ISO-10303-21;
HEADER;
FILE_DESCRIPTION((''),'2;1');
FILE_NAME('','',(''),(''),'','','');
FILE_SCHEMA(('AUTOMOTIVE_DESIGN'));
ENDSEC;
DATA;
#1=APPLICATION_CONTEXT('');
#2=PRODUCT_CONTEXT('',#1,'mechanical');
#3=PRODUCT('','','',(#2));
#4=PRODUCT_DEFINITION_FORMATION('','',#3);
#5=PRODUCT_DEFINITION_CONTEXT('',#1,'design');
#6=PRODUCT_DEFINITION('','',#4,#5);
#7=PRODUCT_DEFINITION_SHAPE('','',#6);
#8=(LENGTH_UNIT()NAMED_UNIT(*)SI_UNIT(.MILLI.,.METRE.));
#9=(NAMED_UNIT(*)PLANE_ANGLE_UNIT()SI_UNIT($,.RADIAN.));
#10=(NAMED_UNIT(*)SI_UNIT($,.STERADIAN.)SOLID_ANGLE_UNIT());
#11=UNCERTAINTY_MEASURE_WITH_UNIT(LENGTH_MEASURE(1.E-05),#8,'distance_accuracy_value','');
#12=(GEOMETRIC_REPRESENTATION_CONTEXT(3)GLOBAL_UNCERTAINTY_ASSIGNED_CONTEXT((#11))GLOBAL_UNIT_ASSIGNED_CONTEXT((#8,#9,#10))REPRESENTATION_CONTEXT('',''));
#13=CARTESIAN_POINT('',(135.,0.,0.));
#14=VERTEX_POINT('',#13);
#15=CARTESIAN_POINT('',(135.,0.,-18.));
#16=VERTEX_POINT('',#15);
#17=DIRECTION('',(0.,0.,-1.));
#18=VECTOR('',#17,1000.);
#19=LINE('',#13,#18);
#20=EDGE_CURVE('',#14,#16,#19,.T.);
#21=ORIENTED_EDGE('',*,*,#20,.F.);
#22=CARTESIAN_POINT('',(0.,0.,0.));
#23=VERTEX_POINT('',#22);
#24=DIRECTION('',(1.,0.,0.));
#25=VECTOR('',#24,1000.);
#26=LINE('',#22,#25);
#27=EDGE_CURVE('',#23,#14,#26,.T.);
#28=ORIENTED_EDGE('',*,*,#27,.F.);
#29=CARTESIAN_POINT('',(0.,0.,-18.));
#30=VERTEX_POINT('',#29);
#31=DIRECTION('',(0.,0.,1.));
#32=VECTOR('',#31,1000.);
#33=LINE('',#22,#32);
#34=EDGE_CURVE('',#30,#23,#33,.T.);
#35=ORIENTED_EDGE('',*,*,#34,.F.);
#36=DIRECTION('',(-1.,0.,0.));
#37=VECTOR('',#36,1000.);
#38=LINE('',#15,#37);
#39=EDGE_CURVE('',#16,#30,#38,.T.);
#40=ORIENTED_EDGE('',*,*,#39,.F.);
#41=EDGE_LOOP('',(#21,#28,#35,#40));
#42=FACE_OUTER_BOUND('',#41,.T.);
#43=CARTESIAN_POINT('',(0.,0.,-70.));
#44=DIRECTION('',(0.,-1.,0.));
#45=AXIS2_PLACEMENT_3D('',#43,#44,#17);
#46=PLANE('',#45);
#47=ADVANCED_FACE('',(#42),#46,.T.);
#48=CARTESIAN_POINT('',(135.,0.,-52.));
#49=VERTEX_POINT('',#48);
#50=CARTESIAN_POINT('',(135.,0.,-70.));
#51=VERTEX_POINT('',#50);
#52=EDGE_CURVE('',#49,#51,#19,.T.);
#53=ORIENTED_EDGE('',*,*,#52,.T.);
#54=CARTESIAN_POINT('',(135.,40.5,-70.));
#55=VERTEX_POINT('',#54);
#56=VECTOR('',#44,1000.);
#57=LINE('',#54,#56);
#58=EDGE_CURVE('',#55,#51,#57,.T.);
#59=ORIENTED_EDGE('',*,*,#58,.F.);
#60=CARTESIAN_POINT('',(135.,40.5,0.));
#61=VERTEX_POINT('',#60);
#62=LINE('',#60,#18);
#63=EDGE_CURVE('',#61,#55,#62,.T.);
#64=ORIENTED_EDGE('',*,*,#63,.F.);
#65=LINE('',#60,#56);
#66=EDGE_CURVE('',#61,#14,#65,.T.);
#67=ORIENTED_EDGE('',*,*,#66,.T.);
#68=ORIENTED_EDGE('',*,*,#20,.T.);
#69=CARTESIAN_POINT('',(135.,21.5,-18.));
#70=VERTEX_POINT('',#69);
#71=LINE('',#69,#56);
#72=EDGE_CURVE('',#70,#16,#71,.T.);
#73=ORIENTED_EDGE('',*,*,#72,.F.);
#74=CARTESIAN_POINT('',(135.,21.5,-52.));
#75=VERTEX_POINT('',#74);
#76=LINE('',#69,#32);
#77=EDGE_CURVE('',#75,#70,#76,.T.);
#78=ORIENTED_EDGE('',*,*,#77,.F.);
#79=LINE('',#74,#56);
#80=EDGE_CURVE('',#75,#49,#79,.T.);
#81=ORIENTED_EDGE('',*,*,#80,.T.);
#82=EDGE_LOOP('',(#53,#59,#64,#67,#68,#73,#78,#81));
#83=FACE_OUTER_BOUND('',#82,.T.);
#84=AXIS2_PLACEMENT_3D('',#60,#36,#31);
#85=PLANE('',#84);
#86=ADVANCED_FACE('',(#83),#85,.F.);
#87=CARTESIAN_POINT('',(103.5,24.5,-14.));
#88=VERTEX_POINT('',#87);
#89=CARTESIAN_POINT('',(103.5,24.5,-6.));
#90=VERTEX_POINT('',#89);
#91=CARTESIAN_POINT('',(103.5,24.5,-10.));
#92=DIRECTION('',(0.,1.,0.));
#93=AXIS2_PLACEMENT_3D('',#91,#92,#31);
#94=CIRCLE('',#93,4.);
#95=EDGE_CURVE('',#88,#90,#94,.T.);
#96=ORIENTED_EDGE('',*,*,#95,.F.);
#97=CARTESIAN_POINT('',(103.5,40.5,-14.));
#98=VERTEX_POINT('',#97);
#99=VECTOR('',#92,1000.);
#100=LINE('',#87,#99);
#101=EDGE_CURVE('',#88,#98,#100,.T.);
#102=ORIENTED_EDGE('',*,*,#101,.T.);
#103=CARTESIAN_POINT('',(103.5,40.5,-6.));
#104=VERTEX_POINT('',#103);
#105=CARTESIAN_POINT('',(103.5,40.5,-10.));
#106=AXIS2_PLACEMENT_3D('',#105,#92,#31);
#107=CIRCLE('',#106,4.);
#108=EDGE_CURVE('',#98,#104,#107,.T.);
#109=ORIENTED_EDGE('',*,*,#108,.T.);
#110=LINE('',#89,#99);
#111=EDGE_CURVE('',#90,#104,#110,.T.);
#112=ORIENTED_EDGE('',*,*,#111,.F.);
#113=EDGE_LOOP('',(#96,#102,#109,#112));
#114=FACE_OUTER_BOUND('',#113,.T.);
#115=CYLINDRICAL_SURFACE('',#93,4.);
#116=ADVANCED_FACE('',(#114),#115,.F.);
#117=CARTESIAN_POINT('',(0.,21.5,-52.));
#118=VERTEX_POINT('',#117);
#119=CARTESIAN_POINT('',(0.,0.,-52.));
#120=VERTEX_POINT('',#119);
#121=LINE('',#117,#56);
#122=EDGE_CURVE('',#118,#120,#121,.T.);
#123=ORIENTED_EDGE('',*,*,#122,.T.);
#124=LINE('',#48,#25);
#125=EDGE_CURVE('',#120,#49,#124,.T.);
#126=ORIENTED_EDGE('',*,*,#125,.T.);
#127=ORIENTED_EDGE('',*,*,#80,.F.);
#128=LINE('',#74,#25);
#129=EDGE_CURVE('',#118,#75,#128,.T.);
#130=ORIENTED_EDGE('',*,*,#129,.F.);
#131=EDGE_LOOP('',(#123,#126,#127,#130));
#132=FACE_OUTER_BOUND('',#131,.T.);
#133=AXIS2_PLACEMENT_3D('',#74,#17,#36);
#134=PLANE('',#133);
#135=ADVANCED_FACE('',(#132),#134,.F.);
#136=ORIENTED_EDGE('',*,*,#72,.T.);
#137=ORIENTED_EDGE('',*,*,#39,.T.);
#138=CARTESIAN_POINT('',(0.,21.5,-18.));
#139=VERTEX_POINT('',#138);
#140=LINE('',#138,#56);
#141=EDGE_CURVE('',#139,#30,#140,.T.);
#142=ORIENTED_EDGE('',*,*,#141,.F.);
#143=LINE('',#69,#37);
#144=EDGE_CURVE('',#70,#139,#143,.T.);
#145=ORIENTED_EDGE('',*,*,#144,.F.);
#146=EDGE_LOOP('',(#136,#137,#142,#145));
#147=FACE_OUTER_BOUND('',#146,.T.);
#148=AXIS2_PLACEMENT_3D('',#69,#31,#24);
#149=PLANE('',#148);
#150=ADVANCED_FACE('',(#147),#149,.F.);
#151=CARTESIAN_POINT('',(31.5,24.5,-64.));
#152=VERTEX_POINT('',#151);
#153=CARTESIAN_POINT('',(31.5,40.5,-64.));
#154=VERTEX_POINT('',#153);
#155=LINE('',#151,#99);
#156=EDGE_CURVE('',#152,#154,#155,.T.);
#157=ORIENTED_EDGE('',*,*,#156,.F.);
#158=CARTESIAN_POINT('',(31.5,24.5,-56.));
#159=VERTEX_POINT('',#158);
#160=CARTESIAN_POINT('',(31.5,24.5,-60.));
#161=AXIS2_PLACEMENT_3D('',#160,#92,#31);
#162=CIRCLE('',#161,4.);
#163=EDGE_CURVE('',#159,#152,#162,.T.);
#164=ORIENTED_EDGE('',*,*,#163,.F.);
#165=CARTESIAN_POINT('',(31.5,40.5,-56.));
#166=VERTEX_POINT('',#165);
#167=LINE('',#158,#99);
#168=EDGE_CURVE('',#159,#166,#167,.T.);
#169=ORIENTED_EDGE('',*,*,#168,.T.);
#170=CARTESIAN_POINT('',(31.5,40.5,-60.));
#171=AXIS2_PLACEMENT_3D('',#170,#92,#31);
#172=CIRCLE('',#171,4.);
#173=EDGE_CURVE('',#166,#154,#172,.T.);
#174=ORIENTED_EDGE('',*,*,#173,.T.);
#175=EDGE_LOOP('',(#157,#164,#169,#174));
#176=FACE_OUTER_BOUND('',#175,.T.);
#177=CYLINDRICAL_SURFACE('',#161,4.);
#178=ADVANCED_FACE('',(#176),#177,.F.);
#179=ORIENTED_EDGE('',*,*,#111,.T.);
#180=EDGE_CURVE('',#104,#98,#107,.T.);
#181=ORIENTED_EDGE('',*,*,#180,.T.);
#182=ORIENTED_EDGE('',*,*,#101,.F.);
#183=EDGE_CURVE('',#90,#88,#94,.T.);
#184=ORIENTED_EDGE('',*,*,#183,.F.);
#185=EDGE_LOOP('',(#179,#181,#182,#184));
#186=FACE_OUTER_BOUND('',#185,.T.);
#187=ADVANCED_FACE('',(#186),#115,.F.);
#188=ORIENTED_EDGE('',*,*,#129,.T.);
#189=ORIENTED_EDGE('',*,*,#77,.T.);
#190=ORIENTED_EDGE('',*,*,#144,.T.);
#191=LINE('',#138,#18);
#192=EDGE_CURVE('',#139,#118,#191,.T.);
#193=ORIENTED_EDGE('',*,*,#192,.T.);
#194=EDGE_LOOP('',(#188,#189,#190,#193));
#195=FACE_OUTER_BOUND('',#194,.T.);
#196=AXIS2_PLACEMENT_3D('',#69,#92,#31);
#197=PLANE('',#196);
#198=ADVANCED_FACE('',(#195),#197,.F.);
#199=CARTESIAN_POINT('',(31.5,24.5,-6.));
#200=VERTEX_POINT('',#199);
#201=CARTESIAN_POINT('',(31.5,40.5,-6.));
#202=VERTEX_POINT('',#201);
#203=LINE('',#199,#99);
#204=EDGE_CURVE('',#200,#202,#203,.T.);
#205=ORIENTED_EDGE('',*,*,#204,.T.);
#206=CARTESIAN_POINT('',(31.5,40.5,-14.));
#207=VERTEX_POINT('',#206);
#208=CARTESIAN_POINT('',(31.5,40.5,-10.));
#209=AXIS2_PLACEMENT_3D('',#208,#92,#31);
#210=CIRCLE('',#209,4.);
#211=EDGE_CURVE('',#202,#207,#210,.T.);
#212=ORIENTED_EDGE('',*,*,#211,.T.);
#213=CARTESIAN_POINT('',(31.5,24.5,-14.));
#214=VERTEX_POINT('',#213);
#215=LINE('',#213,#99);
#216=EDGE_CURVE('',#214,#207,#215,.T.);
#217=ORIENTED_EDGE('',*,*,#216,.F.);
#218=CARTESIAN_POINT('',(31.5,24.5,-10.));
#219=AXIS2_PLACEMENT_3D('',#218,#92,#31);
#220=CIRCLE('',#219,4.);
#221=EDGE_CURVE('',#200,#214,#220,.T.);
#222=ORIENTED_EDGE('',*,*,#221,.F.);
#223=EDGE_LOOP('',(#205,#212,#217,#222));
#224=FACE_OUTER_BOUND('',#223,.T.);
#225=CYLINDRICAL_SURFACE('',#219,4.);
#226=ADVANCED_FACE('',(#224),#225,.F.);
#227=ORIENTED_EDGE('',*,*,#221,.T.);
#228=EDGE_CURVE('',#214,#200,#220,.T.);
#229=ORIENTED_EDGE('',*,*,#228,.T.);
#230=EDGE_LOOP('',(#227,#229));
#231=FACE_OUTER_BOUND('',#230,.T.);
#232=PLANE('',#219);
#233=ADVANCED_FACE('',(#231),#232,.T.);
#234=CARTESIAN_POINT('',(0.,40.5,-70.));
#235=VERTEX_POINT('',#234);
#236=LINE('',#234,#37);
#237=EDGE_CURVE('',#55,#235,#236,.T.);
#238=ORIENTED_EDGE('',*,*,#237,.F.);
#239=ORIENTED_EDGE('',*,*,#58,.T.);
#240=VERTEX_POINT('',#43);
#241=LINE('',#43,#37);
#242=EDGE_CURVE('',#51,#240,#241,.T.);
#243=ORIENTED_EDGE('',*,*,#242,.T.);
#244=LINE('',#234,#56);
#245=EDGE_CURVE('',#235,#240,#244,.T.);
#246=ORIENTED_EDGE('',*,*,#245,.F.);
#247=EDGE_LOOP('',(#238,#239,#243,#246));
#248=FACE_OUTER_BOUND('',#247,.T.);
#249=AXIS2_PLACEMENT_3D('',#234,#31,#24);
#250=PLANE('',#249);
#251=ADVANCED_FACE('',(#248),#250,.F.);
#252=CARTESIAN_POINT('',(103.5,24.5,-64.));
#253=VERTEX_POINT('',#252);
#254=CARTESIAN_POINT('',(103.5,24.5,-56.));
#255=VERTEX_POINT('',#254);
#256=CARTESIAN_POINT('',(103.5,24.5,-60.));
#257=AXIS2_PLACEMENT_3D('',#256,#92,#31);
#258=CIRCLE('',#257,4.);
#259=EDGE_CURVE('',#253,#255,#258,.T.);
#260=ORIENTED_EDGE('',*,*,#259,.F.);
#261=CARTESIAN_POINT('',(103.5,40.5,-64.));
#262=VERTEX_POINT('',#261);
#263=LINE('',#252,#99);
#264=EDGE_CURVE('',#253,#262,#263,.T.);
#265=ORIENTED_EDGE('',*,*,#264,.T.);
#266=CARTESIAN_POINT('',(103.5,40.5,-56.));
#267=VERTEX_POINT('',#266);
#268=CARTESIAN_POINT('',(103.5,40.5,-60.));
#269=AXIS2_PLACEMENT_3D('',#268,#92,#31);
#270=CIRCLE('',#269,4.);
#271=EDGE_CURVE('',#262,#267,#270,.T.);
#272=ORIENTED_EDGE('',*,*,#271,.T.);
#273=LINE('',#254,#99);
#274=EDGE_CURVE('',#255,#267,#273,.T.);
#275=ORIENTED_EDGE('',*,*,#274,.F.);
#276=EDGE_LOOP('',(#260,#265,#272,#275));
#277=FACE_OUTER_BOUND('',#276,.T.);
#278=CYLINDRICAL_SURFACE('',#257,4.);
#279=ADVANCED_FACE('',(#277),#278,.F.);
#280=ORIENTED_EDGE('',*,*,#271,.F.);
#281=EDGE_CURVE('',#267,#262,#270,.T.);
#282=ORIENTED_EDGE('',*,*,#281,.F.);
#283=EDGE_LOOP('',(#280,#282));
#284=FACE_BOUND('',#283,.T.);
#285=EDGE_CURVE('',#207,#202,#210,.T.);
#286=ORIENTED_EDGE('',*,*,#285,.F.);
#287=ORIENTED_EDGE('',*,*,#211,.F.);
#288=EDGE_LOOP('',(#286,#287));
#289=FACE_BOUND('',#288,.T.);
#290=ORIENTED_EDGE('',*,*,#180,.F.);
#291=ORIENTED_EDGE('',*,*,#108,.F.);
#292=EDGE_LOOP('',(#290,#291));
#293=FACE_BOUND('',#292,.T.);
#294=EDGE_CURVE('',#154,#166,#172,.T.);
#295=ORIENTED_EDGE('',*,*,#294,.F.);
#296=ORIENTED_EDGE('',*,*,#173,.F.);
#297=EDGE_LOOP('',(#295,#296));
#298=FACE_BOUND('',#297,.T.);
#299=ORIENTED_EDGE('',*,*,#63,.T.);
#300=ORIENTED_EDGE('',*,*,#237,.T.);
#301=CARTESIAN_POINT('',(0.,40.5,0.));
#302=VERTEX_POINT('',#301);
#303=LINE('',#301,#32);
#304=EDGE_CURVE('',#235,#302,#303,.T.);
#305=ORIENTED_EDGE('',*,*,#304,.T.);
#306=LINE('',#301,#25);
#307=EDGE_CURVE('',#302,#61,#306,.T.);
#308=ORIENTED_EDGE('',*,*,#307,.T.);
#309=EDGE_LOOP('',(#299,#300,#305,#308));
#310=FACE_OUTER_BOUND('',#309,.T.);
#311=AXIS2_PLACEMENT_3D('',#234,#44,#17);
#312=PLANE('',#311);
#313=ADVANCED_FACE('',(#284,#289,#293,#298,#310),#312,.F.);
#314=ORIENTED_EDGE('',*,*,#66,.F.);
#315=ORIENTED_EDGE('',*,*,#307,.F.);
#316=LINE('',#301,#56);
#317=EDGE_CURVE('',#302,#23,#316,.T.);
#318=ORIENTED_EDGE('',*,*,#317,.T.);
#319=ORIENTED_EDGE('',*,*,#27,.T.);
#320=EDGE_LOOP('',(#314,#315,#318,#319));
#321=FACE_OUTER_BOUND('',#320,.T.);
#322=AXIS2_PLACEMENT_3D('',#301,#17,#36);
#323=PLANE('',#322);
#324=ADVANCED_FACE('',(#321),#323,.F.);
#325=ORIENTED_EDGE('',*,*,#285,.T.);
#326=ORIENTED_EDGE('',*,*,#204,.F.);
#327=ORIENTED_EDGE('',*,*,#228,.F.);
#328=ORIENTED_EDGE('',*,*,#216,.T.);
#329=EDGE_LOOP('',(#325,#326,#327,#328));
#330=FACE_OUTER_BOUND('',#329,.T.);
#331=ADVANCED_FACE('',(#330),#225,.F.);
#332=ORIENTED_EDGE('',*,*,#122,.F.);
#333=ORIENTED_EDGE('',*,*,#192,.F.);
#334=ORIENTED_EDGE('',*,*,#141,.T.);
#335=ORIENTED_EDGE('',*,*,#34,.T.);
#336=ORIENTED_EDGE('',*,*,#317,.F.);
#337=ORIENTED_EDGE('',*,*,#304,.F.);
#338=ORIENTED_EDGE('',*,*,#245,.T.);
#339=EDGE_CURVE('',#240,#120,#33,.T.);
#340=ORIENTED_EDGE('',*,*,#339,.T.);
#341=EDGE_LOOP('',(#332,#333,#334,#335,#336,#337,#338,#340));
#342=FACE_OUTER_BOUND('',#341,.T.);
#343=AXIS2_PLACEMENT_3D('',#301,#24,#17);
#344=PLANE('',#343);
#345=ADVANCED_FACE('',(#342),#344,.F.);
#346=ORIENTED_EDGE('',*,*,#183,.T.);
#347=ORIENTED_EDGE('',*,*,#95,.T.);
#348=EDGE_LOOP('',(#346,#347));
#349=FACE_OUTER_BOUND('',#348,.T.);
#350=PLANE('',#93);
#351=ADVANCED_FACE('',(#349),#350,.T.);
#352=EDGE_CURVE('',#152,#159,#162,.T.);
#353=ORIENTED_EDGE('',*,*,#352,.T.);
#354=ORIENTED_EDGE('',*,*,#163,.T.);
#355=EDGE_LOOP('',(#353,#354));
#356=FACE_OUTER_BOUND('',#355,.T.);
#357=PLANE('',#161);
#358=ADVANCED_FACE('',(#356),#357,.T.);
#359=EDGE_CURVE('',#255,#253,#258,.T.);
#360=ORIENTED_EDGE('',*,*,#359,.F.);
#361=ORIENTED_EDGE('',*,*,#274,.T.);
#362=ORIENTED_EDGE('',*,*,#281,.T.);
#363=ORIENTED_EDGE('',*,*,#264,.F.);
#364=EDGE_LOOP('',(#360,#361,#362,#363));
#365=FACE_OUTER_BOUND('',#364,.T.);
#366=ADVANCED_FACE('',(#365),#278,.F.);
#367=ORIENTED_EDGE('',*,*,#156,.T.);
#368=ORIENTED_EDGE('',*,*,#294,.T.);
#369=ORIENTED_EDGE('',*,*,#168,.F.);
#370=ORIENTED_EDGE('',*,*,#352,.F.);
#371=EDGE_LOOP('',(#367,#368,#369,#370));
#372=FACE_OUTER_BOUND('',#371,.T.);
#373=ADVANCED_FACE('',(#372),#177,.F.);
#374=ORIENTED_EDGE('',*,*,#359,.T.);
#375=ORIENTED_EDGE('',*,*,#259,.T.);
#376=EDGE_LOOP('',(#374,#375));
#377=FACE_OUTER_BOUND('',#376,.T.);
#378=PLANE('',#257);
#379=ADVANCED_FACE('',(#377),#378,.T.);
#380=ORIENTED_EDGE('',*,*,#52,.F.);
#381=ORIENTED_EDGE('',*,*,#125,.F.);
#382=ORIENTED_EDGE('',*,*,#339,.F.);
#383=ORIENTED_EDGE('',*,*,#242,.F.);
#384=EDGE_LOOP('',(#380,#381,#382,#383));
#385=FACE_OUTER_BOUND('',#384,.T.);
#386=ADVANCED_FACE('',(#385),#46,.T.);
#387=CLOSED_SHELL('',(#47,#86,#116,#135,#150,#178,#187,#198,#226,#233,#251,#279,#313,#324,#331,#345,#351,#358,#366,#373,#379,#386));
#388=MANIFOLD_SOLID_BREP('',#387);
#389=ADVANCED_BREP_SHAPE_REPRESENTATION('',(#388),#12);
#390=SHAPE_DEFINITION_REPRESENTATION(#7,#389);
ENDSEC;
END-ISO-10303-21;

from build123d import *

# Parameters (mm, degrees)
SKETCH_1_W          = 135
SKETCH_1_H          = 70
EXTRUDE_1_DEPTH     = 40.5
SKETCH_2_W          = 135
SKETCH_2_H          = 34
CUT_EXTRUDE_1_DEPTH = 21.5
SKETCH_3_R          = 4
CUT_EXTRUDE_2_DEPTH = 16


with BuildPart() as part:
    # 草图1 → 拉伸1 (new body)
    with BuildSketch(Plane(origin=(0, 0, 0), x_dir=(1, 0, 0), z_dir=(0, 1, 0))):
        with Locations((67.5, 35)):
            Rectangle(SKETCH_1_W, SKETCH_1_H)
    extrude(amount=EXTRUDE_1_DEPTH)

    # 草图2 → 切除-拉伸1 (cut)
    with BuildSketch(Plane.XZ):
        with Locations((67.5, -35)):
            Rectangle(SKETCH_2_W, SKETCH_2_H)
    extrude(amount=-CUT_EXTRUDE_1_DEPTH, mode=Mode.SUBTRACT)

    # 草图3 → 切除-拉伸2 (cut)
    with BuildSketch(Plane(origin=(0, 40.5, 0), x_dir=(-1, 0, 0), z_dir=(0, 1, 0))):
        with Locations(Location((-103.5, -60, 0), (0, 0, 90))):
            Circle(SKETCH_3_R)
        with Locations(Location((-103.5, -10, 0), (0, 0, 90))):
            Circle(SKETCH_3_R)
        with Locations(Location((-31.5, -60, 0), (0, 0, 90))):
            Circle(SKETCH_3_R)
        with Locations(Location((-31.5, -10, 0), (0, 0, 90))):
            Circle(SKETCH_3_R)
    extrude(amount=-CUT_EXTRUDE_2_DEPTH, mode=Mode.SUBTRACT)


solid = part.part
